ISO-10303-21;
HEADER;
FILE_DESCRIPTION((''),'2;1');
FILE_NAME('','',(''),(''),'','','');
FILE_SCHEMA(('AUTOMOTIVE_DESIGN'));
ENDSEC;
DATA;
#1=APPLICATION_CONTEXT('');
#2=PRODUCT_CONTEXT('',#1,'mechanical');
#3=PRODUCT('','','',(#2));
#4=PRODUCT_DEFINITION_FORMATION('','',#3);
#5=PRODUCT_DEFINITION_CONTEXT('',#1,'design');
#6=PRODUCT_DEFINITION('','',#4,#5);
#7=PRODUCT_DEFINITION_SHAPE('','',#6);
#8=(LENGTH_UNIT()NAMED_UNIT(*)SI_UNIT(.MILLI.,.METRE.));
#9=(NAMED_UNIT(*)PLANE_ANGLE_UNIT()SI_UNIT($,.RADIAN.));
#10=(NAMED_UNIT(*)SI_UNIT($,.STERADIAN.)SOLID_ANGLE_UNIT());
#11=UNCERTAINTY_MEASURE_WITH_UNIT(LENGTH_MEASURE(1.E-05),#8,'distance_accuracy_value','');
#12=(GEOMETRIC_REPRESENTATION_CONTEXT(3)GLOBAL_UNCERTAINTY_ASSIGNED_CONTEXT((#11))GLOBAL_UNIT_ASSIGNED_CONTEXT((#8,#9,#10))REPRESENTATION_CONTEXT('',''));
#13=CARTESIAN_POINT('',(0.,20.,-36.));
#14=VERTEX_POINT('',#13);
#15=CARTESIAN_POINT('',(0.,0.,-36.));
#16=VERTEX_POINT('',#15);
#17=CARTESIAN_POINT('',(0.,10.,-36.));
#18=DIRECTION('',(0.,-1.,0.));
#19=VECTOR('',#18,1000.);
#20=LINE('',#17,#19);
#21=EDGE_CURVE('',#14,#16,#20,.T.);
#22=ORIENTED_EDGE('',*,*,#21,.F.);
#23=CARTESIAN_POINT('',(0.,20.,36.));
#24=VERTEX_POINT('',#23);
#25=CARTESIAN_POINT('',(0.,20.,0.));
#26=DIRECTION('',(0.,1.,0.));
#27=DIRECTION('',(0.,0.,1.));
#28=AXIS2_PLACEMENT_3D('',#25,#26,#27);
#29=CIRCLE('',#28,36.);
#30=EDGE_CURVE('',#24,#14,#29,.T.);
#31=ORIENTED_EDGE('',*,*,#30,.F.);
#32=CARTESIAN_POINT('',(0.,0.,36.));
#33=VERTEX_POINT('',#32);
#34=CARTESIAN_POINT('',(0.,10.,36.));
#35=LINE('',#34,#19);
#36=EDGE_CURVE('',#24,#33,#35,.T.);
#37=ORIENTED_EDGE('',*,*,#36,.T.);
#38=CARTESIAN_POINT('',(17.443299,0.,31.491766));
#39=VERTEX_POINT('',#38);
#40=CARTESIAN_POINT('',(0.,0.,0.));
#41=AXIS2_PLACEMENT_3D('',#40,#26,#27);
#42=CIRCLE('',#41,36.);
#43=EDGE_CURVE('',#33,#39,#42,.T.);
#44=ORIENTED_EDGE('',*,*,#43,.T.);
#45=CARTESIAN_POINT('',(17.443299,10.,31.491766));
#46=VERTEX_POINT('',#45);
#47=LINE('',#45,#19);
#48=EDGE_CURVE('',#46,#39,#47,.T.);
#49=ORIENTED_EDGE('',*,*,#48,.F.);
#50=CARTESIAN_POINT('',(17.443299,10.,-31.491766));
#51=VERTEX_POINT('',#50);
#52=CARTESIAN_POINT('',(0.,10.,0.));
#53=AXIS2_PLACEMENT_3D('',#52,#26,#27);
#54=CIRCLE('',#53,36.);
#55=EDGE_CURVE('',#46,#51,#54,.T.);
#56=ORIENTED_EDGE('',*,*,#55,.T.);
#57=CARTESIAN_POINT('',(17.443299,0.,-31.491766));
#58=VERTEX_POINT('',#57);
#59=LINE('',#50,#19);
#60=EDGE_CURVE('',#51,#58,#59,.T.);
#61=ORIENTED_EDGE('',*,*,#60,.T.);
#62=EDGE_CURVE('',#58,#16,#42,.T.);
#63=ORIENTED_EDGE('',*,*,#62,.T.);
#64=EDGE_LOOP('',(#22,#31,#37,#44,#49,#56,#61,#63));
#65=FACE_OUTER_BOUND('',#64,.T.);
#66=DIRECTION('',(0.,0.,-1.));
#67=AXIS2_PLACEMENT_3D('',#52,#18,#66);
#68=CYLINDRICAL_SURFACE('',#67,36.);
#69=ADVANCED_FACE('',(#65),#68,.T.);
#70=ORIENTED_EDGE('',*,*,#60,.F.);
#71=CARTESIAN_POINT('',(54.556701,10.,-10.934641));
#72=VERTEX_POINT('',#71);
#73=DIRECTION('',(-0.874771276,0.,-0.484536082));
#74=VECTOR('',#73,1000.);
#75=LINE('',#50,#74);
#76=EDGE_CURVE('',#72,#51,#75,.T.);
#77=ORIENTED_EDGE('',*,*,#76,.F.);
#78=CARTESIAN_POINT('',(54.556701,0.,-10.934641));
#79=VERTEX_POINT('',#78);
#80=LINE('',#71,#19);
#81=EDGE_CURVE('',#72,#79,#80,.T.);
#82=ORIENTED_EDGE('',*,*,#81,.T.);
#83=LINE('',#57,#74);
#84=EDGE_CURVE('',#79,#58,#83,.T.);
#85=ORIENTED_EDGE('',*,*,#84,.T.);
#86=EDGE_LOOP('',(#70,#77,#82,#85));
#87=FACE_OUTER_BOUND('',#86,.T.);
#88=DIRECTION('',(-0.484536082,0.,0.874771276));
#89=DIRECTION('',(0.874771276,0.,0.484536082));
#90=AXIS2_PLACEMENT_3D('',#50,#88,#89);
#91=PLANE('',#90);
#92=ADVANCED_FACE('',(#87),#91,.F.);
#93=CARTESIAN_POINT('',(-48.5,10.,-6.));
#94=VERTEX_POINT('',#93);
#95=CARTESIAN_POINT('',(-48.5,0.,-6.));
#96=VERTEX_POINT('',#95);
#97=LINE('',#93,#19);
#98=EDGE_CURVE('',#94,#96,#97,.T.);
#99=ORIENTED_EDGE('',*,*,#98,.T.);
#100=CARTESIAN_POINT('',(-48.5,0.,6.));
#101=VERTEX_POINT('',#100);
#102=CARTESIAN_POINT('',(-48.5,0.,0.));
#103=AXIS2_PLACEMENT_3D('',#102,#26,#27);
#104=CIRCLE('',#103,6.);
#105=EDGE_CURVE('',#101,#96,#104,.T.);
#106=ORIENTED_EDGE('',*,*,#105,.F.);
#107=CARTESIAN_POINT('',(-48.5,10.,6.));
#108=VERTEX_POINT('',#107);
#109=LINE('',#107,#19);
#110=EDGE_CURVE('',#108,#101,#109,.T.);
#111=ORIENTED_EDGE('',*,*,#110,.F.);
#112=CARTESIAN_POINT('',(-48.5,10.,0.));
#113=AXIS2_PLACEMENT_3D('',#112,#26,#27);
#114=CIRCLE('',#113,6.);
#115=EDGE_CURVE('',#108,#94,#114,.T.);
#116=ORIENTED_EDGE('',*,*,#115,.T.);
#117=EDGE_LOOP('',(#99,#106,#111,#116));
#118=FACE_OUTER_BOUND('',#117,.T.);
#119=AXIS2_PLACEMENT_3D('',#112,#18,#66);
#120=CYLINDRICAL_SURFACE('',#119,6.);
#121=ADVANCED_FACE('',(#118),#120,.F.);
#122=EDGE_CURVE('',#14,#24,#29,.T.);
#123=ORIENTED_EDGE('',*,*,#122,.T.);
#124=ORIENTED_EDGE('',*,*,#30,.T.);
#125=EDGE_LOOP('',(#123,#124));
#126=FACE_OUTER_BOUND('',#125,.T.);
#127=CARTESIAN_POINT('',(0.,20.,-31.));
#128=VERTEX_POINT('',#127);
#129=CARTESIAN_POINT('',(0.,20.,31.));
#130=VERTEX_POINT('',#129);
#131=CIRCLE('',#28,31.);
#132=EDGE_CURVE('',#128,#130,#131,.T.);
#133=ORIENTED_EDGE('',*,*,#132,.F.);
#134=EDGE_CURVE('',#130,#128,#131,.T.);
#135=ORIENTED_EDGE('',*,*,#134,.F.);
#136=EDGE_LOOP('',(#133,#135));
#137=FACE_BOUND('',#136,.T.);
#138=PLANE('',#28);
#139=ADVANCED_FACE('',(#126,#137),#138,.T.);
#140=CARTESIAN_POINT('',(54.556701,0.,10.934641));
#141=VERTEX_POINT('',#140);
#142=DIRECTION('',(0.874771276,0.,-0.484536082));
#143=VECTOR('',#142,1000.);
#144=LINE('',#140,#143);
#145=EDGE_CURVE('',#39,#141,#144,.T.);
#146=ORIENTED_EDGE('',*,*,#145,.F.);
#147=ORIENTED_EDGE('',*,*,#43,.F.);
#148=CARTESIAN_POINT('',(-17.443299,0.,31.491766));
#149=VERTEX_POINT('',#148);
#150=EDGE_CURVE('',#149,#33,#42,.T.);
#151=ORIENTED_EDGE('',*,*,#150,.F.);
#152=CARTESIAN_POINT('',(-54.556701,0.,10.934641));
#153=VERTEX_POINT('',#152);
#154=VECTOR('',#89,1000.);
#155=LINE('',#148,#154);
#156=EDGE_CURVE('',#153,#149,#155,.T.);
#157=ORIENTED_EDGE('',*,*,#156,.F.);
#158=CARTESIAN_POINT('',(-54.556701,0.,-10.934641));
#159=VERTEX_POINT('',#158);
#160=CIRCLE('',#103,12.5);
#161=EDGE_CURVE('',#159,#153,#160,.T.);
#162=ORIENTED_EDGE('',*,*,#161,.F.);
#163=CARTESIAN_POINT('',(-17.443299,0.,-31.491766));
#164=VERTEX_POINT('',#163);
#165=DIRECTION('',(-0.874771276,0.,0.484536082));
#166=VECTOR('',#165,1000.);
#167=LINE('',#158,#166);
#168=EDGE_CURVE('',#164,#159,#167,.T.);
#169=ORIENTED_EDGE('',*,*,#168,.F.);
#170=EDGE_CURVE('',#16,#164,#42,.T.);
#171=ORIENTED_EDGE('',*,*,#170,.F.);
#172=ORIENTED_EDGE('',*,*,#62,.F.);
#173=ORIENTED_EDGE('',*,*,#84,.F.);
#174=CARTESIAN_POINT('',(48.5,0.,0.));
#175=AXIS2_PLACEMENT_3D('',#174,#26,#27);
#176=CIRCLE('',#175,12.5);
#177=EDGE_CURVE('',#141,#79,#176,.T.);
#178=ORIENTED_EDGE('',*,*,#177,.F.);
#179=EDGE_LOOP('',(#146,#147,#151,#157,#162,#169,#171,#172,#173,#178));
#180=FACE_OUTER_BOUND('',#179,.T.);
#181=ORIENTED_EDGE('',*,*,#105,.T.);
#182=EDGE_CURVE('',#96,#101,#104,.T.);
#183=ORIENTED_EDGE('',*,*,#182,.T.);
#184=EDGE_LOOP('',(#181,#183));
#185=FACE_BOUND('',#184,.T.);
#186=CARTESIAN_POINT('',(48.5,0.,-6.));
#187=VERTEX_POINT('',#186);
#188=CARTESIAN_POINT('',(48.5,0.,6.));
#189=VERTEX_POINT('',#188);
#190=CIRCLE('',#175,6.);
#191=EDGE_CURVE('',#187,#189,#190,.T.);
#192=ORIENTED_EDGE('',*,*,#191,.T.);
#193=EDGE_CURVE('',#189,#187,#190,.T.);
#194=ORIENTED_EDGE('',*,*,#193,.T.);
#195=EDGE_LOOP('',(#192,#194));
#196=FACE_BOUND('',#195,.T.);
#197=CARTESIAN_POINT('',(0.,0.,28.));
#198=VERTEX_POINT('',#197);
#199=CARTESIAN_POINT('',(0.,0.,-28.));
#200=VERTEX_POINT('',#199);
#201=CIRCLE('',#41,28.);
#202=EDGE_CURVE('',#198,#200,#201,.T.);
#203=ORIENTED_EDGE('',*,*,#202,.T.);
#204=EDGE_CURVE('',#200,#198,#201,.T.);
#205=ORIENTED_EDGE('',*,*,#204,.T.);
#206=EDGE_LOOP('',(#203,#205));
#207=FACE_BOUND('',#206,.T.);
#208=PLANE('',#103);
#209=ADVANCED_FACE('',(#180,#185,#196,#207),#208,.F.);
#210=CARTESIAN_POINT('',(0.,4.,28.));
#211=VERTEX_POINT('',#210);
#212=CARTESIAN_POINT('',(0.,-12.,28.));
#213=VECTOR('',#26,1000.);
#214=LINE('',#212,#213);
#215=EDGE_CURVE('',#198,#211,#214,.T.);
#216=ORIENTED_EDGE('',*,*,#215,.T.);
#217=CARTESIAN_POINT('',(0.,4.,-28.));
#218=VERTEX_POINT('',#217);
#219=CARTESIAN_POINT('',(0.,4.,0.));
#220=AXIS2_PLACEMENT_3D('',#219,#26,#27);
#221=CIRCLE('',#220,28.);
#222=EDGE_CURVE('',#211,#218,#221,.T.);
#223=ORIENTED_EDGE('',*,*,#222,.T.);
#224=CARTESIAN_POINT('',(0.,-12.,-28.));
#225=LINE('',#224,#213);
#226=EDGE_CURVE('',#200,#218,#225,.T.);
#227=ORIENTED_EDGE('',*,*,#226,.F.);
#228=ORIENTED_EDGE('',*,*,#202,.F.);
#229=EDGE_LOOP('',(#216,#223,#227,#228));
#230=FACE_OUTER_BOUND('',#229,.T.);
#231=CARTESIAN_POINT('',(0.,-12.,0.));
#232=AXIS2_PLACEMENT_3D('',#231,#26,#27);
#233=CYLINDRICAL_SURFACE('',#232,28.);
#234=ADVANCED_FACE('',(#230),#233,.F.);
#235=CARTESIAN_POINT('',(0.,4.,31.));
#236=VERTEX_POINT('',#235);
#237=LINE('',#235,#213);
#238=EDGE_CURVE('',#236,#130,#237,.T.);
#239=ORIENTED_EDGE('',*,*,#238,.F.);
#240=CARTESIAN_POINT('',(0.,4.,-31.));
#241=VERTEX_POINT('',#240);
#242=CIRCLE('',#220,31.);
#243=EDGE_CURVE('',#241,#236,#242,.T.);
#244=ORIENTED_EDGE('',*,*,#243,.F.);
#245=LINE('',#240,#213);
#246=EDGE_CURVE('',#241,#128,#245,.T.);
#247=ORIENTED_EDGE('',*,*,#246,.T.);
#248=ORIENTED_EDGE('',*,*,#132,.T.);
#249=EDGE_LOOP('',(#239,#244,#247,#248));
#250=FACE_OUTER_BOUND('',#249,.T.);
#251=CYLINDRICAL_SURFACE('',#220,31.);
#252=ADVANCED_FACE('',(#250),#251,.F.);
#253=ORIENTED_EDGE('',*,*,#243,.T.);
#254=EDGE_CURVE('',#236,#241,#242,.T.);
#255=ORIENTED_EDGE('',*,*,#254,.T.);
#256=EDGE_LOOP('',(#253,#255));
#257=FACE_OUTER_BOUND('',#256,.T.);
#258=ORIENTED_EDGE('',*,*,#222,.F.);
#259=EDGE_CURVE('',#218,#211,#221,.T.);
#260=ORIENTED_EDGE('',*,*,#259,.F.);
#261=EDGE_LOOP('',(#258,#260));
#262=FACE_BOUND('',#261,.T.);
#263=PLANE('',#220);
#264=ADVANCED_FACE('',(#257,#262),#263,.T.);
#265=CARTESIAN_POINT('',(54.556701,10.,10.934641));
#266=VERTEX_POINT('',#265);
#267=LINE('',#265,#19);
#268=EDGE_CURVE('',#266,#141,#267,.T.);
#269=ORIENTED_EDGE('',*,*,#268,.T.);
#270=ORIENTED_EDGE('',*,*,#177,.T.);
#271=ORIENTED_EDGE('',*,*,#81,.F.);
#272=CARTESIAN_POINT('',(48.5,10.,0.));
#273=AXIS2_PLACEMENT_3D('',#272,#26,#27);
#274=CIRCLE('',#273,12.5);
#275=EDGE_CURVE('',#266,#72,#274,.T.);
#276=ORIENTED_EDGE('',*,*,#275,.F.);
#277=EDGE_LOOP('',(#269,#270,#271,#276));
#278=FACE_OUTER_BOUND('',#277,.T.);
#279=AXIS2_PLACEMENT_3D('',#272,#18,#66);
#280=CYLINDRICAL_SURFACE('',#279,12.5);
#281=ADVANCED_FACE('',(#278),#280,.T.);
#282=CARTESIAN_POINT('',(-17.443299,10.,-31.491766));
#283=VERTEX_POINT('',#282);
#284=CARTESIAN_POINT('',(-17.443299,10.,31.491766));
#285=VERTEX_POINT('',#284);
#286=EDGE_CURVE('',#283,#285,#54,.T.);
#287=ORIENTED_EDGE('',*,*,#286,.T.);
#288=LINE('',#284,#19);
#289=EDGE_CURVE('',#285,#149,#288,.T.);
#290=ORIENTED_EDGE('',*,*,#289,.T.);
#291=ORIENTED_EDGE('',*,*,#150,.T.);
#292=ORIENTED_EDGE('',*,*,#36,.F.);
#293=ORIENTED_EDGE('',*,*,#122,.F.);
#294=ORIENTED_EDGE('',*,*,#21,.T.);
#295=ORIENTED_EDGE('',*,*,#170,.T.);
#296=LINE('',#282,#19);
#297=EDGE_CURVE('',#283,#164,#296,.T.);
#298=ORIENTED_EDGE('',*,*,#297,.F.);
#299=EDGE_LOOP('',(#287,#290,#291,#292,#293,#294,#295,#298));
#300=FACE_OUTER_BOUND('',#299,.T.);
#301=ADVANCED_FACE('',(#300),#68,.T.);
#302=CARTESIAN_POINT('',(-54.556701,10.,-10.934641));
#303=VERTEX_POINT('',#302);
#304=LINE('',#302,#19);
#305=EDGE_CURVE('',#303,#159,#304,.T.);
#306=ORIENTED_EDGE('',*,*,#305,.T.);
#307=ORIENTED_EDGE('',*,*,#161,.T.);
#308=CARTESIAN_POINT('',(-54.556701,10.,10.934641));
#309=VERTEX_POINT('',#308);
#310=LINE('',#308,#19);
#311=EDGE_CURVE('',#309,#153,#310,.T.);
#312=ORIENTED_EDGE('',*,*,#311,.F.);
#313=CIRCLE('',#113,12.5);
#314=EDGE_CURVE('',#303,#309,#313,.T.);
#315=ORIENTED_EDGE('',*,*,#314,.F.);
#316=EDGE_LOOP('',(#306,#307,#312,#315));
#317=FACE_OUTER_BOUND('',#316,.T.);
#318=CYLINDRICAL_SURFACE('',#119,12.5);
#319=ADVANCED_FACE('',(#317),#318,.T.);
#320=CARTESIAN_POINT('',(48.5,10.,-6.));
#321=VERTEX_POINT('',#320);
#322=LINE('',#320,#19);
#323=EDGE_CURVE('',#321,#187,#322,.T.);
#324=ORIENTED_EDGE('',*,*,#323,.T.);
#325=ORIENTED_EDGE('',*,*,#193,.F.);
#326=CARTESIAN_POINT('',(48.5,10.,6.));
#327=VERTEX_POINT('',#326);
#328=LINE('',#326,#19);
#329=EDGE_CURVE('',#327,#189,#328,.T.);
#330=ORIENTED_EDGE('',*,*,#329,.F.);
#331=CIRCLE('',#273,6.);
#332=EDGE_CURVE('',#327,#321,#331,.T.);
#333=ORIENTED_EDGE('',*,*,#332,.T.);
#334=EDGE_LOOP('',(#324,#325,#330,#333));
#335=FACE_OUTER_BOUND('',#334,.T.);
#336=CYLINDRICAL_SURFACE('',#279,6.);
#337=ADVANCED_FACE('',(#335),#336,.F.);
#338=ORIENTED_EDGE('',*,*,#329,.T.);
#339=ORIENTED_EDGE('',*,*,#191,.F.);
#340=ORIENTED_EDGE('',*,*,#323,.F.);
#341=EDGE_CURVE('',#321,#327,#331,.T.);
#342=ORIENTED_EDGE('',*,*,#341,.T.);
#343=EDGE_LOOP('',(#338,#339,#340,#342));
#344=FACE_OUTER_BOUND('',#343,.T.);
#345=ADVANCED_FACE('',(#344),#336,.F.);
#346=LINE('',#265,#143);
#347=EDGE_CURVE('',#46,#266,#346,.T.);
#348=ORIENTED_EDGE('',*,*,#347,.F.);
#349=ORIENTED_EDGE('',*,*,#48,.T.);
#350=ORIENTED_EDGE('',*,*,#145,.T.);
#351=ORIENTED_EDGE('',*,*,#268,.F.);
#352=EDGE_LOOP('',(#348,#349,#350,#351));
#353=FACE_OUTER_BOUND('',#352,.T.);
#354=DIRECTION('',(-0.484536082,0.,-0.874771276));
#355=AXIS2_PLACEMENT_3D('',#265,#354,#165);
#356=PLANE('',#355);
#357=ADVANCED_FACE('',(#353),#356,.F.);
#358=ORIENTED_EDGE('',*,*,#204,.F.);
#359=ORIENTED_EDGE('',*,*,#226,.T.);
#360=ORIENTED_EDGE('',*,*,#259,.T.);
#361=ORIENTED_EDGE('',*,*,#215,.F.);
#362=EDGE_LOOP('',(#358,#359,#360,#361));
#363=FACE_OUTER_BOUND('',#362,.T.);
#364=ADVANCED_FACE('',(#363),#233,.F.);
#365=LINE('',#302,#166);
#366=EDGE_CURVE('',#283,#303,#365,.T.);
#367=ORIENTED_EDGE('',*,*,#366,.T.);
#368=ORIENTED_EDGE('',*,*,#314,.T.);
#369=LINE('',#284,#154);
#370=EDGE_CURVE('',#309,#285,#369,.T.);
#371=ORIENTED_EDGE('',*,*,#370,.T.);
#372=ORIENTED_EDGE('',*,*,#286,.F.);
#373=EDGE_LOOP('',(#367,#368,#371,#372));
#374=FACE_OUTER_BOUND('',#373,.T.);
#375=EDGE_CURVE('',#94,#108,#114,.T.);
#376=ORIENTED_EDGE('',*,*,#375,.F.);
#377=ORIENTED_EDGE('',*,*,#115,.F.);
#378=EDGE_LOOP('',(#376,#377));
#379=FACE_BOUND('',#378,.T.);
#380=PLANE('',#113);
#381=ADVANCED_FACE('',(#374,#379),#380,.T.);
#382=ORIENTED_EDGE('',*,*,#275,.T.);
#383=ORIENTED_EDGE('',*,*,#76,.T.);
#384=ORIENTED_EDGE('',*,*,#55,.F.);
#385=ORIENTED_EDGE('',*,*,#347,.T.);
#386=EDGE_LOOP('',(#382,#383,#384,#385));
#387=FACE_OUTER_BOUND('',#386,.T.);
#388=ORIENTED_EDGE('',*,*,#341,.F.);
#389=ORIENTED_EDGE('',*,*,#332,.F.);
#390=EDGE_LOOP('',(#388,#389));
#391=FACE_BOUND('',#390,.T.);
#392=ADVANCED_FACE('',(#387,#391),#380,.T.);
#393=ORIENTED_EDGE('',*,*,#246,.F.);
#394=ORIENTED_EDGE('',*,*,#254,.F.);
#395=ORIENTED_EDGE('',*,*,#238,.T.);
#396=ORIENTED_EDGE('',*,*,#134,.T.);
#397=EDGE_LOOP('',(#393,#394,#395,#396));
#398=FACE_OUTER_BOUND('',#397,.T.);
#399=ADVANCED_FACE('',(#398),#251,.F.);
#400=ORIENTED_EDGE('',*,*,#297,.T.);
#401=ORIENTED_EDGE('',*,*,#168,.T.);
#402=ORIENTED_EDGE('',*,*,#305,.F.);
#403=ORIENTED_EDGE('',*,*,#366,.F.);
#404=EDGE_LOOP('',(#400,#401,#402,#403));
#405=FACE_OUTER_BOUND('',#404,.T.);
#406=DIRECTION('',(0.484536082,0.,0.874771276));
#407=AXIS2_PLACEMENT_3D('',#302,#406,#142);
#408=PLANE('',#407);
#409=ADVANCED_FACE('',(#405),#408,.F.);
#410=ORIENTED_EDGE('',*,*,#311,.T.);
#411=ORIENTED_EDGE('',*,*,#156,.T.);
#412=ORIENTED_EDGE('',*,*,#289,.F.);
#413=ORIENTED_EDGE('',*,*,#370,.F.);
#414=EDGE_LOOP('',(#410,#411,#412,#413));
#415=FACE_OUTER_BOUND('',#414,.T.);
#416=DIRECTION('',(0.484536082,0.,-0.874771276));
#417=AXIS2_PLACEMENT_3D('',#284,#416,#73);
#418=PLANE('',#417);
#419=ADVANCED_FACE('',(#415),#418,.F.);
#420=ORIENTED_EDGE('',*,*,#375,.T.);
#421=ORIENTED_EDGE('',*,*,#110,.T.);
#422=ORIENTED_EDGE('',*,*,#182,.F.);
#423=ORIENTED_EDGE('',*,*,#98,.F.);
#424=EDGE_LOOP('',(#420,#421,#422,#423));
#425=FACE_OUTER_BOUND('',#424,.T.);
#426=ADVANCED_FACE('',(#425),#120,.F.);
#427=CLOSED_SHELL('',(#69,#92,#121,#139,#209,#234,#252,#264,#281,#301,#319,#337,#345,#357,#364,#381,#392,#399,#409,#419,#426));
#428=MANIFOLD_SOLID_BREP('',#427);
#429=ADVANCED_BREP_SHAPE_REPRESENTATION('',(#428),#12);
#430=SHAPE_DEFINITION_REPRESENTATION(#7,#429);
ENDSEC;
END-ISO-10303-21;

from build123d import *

# Parameters (mm, degrees)
SKETCH_1_R          = 6
EXTRUDE_1_DEPTH     = 10
SKETCH_2_R          = 36
EXTRUDE_2_DEPTH     = 10
SKETCH_3_R          = 31
CUT_EXTRUDE_1_DEPTH = 16
SKETCH_4_R          = 28
CUT_EXTRUDE_2_DEPTH = 16


with BuildPart() as part:
    # 草图1 → 凸台-拉伸1 (new body)
    with BuildSketch(Plane(origin=(0, 0, 0), x_dir=(1, 0, 0), z_dir=(0, 1, 0))):
        with BuildLine():
            Line((-54.556701031, 10.934640946), (-17.443298969, 31.491765925))
            ThreePointArc((-17.443298969, 31.491765925), (0, 36), (17.443298969, 31.491765925))
            Line((17.443298969, 31.491765925), (54.556701031, 10.934640946))
            ThreePointArc((54.556701031, 10.934640946), (61, 0), (54.556701031, -10.934640946))
            Line((54.556701031, -10.934640946), (17.443298969, -31.491765925))
            ThreePointArc((17.443298969, -31.491765925), (0, -36), (-17.443298969, -31.491765925))
            Line((-17.443298969, -31.491765925), (-54.556701031, -10.934640946))
            ThreePointArc((-54.556701031, -10.934640946), (-61, 0), (-54.556701031, 10.934640946))
        make_face()
        with Locations(Location((48.5, 0, 0), (0, 0, 270))):
            Circle(SKETCH_1_R, mode=Mode.SUBTRACT)
        with Locations(Location((-48.5, 0, 0), (0, 0, 270))):
            Circle(SKETCH_1_R, mode=Mode.SUBTRACT)
    extrude(amount=EXTRUDE_1_DEPTH)

    # 草图2 → 凸台-拉伸2 (add)
    with BuildSketch(Plane(origin=(0, 10, 0), x_dir=(1, 0, 0), z_dir=(0, 1, 0))):
        with Locations(Location((0, 0, 0), (0, 0, 118.982082268))):
            Circle(SKETCH_2_R)
    extrude(amount=EXTRUDE_2_DEPTH)

    # 草图3 → 切除-拉伸1 (cut)
    with BuildSketch(Plane(origin=(0, 20, 0), x_dir=(1, 0, 0), z_dir=(0, 1, 0))):
        with Locations(Location((0, 0, 0), (0, 0, 270))):
            Circle(SKETCH_3_R)
    extrude(amount=-CUT_EXTRUDE_1_DEPTH, mode=Mode.SUBTRACT)

    # 草图4 → 切除-拉伸2 (cut)
    with BuildSketch(Plane(origin=(0, 4, 0), x_dir=(1, 0, 0), z_dir=(0, 1, 0))):
        with Locations(Location((0, 0, 0), (0, 0, 270))):
            Circle(SKETCH_4_R)
    extrude(amount=-CUT_EXTRUDE_2_DEPTH, mode=Mode.SUBTRACT)


solid = part.part
